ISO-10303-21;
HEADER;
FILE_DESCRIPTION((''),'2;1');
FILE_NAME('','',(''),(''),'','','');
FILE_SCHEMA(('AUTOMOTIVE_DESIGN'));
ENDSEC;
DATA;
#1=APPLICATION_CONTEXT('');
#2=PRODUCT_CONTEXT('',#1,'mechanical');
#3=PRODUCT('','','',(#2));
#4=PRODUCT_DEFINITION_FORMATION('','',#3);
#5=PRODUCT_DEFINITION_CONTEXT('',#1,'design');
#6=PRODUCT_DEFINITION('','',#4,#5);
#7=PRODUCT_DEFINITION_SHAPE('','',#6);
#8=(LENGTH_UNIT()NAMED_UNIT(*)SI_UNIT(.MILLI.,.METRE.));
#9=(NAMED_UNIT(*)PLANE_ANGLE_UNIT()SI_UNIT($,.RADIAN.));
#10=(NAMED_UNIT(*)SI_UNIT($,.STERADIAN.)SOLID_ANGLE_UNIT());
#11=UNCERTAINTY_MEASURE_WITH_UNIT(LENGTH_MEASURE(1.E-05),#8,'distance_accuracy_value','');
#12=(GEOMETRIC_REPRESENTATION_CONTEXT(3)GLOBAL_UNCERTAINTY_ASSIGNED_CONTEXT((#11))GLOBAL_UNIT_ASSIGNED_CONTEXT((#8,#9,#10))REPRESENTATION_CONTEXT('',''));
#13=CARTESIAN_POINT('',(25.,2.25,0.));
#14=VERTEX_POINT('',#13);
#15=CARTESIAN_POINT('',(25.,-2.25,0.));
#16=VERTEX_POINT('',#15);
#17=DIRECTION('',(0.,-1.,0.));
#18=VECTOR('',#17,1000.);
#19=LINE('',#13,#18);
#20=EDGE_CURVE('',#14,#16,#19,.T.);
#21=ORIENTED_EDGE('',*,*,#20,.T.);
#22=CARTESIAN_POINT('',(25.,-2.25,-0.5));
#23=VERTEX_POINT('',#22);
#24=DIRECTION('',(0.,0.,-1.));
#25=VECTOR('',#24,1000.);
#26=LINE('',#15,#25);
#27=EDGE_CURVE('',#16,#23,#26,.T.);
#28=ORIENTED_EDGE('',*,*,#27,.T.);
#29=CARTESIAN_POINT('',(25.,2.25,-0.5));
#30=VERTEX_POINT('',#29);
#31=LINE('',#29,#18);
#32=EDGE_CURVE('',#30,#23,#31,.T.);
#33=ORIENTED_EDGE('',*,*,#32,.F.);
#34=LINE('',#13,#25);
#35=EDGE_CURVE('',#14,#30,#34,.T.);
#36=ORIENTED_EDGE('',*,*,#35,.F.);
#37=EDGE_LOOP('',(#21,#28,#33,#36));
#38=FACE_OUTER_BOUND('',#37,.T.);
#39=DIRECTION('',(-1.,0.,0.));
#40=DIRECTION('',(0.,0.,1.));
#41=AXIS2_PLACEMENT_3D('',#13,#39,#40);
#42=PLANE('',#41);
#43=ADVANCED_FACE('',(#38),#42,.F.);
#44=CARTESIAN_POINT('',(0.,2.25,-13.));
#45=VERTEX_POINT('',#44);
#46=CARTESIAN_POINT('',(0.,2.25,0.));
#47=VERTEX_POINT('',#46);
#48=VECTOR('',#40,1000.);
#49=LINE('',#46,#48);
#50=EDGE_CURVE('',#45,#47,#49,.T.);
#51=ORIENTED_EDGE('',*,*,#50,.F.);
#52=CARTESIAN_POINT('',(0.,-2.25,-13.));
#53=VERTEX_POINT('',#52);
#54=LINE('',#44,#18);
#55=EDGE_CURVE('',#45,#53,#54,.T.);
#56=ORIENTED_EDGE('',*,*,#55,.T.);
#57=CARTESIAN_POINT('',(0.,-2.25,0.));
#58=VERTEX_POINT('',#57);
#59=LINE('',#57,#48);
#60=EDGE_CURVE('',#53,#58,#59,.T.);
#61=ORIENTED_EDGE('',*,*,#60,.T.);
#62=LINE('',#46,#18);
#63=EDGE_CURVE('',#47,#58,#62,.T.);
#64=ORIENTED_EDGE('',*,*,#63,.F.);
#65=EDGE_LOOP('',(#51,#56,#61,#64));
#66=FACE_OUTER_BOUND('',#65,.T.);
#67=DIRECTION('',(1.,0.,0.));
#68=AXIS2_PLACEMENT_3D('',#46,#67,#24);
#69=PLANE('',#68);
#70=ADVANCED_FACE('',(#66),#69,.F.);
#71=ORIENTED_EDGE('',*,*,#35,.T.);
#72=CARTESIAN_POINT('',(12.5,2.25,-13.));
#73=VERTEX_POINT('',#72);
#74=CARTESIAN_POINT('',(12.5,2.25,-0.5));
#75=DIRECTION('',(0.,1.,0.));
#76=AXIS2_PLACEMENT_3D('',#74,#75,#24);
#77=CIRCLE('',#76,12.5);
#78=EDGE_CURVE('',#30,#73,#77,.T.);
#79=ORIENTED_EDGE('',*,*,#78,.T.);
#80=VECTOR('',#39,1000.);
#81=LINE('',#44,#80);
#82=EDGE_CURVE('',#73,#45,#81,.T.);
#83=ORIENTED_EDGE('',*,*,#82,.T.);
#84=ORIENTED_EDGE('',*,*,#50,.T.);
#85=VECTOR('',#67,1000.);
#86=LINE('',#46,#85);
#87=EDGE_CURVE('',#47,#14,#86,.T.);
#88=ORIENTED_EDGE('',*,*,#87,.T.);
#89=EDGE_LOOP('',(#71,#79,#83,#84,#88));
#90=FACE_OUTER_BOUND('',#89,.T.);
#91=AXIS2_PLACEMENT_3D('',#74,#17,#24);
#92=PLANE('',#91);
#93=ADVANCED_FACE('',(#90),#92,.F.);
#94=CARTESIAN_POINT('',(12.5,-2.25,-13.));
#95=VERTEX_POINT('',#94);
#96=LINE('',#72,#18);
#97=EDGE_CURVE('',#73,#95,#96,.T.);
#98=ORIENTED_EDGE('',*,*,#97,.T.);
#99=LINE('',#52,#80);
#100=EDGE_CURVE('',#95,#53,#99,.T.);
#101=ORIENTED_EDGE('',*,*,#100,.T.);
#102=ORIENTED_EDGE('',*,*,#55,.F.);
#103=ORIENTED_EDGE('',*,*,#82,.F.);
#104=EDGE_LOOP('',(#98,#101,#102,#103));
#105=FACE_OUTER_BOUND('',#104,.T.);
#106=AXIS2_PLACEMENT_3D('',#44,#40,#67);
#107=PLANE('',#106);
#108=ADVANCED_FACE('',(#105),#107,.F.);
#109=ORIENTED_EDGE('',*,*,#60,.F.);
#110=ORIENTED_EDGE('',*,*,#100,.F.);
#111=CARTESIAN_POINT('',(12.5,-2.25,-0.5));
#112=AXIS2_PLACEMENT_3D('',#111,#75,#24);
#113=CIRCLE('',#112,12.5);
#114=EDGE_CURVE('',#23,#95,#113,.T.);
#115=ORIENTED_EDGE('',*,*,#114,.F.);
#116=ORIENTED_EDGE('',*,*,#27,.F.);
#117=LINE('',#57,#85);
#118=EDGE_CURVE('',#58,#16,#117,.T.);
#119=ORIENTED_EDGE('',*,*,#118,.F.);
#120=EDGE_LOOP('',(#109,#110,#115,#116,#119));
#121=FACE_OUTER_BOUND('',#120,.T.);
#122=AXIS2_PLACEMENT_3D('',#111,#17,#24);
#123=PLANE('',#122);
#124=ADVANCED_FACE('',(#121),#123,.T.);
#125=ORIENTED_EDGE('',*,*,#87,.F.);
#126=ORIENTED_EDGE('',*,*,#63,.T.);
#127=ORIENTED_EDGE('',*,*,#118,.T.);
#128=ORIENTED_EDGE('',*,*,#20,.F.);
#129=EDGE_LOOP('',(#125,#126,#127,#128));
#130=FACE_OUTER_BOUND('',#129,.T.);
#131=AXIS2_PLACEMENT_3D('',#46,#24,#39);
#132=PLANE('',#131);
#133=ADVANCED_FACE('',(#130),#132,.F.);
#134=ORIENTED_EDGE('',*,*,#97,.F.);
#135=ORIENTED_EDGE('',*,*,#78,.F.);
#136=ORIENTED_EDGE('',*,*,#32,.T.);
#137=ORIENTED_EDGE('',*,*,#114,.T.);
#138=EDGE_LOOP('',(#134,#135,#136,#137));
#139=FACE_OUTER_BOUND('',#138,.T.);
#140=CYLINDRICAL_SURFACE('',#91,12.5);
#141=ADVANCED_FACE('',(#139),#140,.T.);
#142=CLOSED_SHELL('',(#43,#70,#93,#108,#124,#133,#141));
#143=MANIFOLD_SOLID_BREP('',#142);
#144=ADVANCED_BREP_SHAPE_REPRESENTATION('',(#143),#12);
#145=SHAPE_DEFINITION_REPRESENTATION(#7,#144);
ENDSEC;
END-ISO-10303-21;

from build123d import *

# Parameters (mm, degrees)
BOSS_EXTRUDE1_DEPTH = 2.25


with BuildPart() as part:
    # Sketch1 → Boss-Extrude1 (new, symmetric)
    with BuildSketch(Plane(origin=(0, 0, 0), x_dir=(1, 0, 0), z_dir=(0, 1, 0))):
        with BuildLine():
            Line((0, 0), (25, 0))
            Line((25, 0), (25, 0.5))
            ThreePointArc((25, 0.5), (21.338834765, 9.338834765), (12.5, 13))
            Line((12.5, 13), (0, 13))
            Line((0, 13), (0, 0))
        make_face()
    extrude(amount=BOSS_EXTRUDE1_DEPTH, both=True)


solid = part.part
